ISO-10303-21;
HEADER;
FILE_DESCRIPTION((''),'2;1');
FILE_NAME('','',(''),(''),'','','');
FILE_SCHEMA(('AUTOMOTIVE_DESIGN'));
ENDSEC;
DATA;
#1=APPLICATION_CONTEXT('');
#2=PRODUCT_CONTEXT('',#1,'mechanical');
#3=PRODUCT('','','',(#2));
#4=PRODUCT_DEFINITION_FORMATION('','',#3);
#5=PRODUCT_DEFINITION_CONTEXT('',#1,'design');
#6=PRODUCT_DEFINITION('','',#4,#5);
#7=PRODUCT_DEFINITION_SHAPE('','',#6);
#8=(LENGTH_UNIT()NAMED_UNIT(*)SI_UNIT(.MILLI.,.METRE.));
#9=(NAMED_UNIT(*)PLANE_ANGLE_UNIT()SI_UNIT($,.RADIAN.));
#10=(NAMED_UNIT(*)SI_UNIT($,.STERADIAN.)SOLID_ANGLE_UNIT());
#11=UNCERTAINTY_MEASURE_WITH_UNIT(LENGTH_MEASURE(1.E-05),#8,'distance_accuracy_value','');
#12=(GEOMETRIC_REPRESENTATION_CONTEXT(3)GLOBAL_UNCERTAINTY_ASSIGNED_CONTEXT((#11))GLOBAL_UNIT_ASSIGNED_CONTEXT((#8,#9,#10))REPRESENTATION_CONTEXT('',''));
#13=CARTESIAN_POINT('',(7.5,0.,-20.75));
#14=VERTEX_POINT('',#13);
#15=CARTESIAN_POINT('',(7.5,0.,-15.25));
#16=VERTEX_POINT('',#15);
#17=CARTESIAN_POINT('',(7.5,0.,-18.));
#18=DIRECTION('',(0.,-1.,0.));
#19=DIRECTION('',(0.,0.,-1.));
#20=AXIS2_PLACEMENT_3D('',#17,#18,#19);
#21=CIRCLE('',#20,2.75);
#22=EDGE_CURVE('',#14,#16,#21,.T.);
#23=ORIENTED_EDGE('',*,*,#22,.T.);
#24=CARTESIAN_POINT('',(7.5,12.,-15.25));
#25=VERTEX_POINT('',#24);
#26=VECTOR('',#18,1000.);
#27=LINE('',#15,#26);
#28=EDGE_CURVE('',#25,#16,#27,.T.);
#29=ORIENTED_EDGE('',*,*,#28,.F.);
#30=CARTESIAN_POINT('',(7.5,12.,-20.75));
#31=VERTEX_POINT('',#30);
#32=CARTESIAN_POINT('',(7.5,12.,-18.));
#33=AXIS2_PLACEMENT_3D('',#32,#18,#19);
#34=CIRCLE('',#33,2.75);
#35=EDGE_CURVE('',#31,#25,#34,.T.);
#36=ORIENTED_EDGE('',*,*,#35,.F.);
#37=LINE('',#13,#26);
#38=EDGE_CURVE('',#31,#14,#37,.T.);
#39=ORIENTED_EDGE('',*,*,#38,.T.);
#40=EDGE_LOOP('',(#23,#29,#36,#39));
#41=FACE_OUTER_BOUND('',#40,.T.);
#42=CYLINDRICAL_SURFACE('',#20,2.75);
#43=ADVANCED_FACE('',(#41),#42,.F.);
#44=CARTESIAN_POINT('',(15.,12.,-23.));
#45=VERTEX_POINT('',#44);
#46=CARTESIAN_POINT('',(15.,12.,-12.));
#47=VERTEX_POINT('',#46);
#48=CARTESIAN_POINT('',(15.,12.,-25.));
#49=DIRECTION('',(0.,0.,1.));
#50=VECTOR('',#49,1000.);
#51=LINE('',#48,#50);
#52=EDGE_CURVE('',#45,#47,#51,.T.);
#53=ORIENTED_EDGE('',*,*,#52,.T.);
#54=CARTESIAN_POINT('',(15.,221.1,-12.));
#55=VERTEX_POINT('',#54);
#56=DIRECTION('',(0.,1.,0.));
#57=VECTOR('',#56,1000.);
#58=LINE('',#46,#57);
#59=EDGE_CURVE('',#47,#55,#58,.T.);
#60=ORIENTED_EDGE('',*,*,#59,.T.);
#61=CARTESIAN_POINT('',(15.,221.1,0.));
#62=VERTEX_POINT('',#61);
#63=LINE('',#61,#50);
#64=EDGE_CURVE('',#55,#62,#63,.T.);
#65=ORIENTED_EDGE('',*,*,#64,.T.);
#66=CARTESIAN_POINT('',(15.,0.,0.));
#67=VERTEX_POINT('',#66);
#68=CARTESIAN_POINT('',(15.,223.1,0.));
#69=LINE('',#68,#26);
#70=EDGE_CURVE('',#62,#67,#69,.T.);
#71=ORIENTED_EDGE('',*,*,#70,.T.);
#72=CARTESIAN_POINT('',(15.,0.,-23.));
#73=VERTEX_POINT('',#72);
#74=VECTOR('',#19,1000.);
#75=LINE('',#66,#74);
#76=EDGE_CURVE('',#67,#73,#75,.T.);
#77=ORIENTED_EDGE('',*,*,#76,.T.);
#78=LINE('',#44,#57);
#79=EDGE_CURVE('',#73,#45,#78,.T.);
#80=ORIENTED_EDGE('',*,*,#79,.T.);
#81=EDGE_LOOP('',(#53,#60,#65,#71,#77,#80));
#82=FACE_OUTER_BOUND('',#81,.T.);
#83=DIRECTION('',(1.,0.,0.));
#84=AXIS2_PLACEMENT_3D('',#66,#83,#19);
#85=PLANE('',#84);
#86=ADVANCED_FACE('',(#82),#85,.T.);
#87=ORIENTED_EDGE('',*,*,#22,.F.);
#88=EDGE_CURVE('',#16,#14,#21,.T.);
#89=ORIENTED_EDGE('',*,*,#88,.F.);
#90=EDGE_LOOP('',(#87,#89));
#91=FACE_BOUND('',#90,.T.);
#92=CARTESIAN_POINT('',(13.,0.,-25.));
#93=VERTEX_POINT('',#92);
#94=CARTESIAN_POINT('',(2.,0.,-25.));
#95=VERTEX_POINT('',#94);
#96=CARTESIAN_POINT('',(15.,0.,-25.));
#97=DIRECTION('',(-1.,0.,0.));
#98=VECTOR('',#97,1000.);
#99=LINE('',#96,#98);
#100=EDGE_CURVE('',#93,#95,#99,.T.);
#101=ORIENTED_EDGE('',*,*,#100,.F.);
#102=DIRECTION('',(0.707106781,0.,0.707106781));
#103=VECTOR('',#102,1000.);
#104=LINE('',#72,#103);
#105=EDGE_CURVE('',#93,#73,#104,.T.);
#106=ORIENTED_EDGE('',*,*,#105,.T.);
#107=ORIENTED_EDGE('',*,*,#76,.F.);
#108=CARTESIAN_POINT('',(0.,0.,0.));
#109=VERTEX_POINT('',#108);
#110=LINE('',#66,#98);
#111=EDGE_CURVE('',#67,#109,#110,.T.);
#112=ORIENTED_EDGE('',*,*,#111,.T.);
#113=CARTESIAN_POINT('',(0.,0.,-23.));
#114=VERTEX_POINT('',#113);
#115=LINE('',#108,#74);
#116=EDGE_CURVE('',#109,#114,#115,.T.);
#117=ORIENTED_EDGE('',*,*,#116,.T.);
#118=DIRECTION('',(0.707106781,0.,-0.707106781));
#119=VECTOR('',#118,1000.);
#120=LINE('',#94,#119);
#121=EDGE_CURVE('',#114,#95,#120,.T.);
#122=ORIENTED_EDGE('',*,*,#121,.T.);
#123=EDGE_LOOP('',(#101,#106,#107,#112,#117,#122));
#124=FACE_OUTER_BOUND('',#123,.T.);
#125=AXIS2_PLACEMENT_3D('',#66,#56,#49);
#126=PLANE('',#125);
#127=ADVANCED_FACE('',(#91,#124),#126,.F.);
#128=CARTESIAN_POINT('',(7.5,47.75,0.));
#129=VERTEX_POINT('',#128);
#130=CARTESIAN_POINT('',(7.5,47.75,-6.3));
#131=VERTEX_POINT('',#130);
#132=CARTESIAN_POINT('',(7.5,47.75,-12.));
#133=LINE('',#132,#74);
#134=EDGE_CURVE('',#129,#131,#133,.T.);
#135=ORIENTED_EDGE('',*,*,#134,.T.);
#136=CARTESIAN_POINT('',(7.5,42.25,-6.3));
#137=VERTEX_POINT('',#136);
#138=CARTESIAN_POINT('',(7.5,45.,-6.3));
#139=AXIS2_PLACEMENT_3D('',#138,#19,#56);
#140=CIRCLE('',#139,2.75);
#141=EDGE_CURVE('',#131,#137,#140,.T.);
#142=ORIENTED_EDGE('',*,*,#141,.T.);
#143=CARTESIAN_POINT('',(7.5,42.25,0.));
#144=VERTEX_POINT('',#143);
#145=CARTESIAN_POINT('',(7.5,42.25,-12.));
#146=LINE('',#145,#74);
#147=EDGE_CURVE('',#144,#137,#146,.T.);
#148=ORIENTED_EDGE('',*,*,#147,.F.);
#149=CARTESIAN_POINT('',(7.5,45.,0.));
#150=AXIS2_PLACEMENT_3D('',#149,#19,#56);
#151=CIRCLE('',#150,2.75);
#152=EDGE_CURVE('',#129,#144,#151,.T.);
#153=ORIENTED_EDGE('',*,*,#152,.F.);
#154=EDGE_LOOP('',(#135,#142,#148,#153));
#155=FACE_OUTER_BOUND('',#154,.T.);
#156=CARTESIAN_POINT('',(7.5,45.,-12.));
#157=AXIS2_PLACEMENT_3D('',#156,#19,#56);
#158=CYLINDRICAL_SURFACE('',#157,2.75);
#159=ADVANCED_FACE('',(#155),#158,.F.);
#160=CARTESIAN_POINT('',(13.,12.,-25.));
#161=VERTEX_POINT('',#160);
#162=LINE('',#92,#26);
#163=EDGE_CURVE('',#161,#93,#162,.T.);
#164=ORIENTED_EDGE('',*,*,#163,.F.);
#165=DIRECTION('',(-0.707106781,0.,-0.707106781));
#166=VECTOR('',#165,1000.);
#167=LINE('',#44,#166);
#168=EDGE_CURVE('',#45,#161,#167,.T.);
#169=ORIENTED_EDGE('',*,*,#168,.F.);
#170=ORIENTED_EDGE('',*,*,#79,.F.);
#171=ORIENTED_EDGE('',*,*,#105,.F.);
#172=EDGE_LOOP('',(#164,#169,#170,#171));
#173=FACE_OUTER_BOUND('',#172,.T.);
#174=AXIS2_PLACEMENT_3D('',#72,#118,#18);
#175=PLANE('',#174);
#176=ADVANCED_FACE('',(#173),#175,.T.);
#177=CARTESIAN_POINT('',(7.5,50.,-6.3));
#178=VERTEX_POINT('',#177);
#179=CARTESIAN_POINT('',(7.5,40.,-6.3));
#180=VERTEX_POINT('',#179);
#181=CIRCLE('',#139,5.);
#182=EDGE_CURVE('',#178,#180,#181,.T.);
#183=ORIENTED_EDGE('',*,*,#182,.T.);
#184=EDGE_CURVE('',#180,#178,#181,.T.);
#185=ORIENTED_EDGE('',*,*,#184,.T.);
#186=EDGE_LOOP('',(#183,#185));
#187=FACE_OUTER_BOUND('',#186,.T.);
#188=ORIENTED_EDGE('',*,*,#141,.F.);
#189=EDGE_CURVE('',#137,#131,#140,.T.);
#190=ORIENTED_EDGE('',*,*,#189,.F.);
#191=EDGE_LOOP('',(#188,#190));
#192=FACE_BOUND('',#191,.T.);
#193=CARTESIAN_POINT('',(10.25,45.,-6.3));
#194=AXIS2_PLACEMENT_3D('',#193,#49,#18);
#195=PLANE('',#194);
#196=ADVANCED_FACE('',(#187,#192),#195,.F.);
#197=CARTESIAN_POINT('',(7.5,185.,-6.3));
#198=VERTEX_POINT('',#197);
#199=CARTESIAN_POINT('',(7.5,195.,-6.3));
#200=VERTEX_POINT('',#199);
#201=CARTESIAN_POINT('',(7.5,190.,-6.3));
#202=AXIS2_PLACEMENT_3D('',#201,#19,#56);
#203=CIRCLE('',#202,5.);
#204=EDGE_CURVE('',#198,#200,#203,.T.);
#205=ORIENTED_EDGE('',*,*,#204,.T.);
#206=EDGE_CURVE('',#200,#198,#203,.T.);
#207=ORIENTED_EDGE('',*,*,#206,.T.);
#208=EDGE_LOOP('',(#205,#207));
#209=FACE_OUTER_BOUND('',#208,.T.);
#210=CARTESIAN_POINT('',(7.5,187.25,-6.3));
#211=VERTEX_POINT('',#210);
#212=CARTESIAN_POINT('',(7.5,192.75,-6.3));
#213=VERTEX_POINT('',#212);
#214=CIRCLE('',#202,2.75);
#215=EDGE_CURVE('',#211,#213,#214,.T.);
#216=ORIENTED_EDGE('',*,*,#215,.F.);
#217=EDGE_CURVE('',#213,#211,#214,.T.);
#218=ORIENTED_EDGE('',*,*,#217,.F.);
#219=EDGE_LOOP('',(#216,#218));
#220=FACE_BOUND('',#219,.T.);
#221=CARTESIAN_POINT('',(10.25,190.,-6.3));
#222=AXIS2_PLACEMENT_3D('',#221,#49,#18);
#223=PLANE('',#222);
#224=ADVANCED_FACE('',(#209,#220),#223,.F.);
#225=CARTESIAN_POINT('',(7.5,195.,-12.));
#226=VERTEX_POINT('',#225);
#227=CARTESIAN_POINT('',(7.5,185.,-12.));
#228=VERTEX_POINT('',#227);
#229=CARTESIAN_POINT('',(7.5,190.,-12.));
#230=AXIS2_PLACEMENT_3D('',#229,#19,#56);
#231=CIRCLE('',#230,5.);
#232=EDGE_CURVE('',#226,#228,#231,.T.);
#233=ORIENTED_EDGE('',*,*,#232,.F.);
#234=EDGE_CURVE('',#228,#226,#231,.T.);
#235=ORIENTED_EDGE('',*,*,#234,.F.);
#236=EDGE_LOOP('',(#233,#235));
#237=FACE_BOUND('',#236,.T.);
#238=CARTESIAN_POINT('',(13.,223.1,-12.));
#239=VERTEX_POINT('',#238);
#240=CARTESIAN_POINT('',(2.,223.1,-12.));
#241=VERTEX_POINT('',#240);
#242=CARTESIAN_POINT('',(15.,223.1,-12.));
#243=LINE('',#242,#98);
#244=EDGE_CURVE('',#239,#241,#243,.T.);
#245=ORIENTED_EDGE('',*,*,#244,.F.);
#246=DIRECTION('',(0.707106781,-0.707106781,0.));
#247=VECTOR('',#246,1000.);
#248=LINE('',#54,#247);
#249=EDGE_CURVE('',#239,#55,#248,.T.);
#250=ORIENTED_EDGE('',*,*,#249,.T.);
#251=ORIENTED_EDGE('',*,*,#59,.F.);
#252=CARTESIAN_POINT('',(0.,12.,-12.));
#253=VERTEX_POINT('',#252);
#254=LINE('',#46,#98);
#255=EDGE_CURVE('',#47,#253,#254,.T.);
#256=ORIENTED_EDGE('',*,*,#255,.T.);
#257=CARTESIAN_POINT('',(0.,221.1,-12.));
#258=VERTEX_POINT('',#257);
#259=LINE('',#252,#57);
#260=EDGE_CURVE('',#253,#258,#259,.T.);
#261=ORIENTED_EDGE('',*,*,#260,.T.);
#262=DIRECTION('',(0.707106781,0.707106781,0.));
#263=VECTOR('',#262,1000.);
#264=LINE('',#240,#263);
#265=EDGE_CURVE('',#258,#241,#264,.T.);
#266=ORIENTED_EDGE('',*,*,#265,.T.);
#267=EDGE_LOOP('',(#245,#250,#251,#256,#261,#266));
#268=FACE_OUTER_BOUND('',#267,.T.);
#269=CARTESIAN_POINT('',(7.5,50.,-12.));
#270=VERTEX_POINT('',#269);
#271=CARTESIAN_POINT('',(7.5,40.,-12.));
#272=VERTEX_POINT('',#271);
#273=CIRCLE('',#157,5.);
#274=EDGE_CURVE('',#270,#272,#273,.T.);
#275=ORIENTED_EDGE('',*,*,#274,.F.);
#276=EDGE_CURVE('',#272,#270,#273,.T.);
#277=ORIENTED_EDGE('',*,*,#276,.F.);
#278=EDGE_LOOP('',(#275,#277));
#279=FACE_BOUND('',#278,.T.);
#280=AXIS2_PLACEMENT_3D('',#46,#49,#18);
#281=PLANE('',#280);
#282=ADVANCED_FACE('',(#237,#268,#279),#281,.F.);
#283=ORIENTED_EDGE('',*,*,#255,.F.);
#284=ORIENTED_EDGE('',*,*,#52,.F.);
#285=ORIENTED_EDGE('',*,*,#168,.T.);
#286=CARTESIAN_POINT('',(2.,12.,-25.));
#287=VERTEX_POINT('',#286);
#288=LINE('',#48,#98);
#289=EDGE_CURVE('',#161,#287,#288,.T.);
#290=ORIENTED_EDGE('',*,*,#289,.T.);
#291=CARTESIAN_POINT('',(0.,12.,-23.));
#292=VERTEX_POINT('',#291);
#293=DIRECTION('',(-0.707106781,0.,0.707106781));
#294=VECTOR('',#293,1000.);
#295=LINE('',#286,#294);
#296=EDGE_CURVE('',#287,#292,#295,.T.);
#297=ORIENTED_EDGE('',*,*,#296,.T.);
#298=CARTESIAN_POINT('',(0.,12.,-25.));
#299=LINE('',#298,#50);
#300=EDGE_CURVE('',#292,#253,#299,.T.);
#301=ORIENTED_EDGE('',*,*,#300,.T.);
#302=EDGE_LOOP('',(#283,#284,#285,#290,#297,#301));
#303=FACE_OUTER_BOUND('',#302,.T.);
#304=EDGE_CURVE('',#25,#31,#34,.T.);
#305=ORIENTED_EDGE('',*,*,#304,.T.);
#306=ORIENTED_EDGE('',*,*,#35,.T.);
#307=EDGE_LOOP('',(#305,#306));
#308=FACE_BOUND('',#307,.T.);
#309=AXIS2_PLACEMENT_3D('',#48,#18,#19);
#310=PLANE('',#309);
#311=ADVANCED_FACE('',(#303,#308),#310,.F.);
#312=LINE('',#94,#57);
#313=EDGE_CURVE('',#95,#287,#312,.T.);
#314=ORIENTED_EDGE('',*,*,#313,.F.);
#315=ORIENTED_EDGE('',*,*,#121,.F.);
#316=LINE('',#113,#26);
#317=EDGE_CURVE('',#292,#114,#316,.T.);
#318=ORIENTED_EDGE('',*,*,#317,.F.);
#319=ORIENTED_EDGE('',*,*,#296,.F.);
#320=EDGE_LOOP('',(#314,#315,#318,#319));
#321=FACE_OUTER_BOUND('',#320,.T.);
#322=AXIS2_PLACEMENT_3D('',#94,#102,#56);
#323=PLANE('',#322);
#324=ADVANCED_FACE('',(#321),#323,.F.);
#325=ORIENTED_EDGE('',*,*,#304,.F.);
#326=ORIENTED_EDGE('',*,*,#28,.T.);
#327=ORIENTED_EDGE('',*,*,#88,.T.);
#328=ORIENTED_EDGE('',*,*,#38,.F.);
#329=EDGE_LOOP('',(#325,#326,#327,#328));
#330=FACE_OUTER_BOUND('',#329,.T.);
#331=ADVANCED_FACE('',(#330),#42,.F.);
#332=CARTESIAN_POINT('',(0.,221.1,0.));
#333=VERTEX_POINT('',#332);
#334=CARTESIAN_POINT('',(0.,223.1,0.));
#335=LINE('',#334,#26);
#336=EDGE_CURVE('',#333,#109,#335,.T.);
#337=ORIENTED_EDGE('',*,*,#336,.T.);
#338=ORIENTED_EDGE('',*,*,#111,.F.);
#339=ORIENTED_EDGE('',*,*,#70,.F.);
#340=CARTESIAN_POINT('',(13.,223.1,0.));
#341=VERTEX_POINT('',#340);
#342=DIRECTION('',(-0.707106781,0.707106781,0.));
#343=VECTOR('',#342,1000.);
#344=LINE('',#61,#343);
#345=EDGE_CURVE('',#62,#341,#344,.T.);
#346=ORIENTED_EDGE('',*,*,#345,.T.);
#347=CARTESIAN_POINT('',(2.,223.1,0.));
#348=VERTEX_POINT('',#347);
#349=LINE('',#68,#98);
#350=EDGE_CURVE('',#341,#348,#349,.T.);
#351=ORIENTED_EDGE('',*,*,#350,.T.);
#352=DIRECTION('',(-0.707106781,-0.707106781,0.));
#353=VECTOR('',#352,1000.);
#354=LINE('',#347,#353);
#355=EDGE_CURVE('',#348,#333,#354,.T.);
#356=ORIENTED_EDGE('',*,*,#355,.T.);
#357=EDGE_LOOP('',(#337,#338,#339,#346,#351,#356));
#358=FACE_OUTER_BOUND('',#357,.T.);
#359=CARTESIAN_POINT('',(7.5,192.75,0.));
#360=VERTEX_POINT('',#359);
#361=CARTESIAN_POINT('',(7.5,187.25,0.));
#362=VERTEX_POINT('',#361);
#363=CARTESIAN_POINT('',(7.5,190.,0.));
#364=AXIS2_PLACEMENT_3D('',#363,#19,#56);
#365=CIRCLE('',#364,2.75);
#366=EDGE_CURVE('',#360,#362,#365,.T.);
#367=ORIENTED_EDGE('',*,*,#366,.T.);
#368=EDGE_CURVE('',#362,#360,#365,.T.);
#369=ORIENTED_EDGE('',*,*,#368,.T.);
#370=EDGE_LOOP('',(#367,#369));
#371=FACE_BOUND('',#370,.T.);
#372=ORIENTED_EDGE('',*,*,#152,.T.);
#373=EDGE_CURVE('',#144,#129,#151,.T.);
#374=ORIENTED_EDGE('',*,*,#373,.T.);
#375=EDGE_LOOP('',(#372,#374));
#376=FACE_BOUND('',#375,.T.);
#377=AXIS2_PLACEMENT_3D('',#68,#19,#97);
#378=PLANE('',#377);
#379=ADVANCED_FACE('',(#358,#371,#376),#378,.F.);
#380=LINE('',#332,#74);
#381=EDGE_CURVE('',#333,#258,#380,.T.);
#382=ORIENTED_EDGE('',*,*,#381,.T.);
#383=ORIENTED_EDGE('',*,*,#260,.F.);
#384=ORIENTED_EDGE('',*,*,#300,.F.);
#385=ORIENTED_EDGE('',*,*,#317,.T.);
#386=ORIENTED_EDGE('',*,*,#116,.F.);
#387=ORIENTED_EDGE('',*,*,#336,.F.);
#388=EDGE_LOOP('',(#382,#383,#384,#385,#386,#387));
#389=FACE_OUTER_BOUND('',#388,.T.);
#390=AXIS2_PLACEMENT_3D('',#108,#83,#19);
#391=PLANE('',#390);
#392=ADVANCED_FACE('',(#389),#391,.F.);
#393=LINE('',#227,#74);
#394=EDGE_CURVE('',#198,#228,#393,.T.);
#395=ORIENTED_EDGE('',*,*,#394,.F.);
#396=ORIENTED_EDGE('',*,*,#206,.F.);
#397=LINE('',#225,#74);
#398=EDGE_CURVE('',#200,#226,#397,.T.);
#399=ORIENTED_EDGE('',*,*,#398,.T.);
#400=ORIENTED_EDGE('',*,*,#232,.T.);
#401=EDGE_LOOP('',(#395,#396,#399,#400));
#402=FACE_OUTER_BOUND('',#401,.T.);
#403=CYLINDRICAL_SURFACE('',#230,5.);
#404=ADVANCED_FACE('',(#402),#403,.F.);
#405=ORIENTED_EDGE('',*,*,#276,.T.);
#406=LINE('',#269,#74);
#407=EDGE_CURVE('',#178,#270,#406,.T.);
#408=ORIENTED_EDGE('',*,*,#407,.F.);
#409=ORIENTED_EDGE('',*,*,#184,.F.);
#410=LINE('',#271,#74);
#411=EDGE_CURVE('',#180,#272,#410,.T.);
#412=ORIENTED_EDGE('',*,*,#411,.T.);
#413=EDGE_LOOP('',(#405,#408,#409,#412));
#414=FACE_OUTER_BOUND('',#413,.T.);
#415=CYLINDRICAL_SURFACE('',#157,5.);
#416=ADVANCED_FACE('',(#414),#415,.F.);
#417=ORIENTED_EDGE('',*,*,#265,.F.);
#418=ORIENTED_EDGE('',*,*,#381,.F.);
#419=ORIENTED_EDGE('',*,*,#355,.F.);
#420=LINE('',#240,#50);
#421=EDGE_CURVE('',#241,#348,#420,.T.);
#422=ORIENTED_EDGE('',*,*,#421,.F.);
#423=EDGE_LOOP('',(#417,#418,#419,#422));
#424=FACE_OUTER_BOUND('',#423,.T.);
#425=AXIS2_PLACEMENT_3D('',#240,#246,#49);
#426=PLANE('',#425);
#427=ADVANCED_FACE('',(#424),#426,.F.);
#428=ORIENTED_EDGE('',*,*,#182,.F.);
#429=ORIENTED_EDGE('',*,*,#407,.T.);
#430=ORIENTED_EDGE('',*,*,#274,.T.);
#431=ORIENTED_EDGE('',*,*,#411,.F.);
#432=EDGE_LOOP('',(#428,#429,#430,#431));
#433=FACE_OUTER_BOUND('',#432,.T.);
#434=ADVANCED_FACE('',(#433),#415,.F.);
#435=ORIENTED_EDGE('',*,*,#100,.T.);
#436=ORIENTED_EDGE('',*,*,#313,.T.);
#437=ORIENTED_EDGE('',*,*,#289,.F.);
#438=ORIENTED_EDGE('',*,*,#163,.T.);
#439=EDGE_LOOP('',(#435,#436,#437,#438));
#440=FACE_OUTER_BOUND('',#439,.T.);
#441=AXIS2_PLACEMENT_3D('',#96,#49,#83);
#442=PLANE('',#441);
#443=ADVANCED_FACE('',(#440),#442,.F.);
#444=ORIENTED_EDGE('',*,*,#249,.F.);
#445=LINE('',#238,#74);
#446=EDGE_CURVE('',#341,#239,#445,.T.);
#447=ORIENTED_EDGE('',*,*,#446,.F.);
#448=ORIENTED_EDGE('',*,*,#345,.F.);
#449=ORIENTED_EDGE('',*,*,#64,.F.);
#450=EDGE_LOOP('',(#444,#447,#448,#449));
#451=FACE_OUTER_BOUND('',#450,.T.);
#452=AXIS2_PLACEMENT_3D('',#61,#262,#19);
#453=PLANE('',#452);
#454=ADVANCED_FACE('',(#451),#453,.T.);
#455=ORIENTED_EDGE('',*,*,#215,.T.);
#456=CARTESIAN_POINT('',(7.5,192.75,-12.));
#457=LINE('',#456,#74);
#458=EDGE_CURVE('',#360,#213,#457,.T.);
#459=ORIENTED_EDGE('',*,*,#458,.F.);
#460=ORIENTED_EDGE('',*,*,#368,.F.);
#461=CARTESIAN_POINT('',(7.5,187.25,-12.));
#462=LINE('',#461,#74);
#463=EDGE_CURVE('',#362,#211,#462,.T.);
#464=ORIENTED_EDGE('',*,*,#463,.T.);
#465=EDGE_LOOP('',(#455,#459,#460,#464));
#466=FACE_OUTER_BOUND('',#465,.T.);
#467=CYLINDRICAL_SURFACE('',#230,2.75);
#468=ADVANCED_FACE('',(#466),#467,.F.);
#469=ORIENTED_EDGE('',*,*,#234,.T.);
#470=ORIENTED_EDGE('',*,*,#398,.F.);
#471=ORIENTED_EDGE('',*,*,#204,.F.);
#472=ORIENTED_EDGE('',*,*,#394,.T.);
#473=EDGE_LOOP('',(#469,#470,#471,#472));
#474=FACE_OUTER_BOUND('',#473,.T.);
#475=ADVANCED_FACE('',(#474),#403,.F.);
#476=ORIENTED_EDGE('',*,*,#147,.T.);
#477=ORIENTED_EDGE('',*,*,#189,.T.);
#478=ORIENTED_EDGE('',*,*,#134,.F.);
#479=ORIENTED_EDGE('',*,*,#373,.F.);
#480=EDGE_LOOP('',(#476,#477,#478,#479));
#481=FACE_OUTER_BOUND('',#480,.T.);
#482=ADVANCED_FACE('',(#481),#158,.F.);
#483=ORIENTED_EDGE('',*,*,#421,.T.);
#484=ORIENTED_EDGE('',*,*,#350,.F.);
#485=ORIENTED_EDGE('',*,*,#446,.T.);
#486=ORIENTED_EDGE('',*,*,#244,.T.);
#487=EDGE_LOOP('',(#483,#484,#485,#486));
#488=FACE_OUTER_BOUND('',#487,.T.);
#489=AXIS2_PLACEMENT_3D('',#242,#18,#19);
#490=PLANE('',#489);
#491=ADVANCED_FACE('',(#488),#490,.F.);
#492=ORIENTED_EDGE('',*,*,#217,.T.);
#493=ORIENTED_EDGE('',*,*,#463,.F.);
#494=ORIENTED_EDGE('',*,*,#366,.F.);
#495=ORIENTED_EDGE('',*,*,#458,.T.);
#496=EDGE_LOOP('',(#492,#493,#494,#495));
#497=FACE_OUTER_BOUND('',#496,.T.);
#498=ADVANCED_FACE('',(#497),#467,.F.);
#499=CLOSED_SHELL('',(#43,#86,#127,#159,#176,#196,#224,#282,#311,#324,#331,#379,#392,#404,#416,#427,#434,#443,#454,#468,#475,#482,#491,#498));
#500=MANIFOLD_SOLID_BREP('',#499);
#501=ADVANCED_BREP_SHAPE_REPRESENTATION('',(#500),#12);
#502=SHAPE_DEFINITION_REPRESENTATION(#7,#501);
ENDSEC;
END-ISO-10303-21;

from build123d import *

# Parameters (mm, degrees)
BOSS_EXTRUDE1_DEPTH                                  = 15
CBORE_FOR_M5_HEXAGON_SOCKET_HEAD_CAP_SCR_D           = 5.5
CBORE_FOR_M5_HEXAGON_SOCKET_HEAD_CAP_SCR_CBORE_D     = 10
CBORE_FOR_M5_HEXAGON_SOCKET_HEAD_CAP_SCR_CBORE_DEPTH = 5.7
M5_CLEARANCE_HOLE1_D                                 = 5.5
CHAMFER1_SIZE                                        = 2


with BuildPart() as part:
    # Sketch1 → Boss-Extrude1 (new body)
    with BuildSketch(Plane(origin=(0, 0, 0), x_dir=(0, 0, -1), z_dir=(1, 0, 0))):
        Polygon((0, 0), (25, 0), (25, 12), (12, 12), (12, 223.1), (0, 223.1), align=None)
    extrude(amount=BOSS_EXTRUDE1_DEPTH)

    # CBORE for M5 Hexagon socket head cap screws1 (through all)
    with Locations(Plane(origin=(0, 0, -12), x_dir=(-1, 0, 0), z_dir=(0, 0, -1))):
        with Locations((-7.5, 45), (-7.5, 190)):
            CounterBoreHole(CBORE_FOR_M5_HEXAGON_SOCKET_HEAD_CAP_SCR_D / 2, CBORE_FOR_M5_HEXAGON_SOCKET_HEAD_CAP_SCR_CBORE_D / 2, CBORE_FOR_M5_HEXAGON_SOCKET_HEAD_CAP_SCR_CBORE_DEPTH)

    # M5 Clearance Hole1 (through all)
    with Locations(Plane(origin=(0, 0, 0), x_dir=(-1, 0, 0), z_dir=(0, -1, 0))):
        with Locations((-7.5, 18)):
            Hole(M5_CLEARANCE_HOLE1_D / 2)

    # Chamfer1
    chamfer1_edges = [part.edges().sort_by_distance(p)[0] for p in [
        (15, 6, -25),
        (15, 223.1, -6),
        (0, 223.1, -6),
        (0, 6, -25),
    ]]
    chamfer(chamfer1_edges, length=CHAMFER1_SIZE)


solid = part.part
